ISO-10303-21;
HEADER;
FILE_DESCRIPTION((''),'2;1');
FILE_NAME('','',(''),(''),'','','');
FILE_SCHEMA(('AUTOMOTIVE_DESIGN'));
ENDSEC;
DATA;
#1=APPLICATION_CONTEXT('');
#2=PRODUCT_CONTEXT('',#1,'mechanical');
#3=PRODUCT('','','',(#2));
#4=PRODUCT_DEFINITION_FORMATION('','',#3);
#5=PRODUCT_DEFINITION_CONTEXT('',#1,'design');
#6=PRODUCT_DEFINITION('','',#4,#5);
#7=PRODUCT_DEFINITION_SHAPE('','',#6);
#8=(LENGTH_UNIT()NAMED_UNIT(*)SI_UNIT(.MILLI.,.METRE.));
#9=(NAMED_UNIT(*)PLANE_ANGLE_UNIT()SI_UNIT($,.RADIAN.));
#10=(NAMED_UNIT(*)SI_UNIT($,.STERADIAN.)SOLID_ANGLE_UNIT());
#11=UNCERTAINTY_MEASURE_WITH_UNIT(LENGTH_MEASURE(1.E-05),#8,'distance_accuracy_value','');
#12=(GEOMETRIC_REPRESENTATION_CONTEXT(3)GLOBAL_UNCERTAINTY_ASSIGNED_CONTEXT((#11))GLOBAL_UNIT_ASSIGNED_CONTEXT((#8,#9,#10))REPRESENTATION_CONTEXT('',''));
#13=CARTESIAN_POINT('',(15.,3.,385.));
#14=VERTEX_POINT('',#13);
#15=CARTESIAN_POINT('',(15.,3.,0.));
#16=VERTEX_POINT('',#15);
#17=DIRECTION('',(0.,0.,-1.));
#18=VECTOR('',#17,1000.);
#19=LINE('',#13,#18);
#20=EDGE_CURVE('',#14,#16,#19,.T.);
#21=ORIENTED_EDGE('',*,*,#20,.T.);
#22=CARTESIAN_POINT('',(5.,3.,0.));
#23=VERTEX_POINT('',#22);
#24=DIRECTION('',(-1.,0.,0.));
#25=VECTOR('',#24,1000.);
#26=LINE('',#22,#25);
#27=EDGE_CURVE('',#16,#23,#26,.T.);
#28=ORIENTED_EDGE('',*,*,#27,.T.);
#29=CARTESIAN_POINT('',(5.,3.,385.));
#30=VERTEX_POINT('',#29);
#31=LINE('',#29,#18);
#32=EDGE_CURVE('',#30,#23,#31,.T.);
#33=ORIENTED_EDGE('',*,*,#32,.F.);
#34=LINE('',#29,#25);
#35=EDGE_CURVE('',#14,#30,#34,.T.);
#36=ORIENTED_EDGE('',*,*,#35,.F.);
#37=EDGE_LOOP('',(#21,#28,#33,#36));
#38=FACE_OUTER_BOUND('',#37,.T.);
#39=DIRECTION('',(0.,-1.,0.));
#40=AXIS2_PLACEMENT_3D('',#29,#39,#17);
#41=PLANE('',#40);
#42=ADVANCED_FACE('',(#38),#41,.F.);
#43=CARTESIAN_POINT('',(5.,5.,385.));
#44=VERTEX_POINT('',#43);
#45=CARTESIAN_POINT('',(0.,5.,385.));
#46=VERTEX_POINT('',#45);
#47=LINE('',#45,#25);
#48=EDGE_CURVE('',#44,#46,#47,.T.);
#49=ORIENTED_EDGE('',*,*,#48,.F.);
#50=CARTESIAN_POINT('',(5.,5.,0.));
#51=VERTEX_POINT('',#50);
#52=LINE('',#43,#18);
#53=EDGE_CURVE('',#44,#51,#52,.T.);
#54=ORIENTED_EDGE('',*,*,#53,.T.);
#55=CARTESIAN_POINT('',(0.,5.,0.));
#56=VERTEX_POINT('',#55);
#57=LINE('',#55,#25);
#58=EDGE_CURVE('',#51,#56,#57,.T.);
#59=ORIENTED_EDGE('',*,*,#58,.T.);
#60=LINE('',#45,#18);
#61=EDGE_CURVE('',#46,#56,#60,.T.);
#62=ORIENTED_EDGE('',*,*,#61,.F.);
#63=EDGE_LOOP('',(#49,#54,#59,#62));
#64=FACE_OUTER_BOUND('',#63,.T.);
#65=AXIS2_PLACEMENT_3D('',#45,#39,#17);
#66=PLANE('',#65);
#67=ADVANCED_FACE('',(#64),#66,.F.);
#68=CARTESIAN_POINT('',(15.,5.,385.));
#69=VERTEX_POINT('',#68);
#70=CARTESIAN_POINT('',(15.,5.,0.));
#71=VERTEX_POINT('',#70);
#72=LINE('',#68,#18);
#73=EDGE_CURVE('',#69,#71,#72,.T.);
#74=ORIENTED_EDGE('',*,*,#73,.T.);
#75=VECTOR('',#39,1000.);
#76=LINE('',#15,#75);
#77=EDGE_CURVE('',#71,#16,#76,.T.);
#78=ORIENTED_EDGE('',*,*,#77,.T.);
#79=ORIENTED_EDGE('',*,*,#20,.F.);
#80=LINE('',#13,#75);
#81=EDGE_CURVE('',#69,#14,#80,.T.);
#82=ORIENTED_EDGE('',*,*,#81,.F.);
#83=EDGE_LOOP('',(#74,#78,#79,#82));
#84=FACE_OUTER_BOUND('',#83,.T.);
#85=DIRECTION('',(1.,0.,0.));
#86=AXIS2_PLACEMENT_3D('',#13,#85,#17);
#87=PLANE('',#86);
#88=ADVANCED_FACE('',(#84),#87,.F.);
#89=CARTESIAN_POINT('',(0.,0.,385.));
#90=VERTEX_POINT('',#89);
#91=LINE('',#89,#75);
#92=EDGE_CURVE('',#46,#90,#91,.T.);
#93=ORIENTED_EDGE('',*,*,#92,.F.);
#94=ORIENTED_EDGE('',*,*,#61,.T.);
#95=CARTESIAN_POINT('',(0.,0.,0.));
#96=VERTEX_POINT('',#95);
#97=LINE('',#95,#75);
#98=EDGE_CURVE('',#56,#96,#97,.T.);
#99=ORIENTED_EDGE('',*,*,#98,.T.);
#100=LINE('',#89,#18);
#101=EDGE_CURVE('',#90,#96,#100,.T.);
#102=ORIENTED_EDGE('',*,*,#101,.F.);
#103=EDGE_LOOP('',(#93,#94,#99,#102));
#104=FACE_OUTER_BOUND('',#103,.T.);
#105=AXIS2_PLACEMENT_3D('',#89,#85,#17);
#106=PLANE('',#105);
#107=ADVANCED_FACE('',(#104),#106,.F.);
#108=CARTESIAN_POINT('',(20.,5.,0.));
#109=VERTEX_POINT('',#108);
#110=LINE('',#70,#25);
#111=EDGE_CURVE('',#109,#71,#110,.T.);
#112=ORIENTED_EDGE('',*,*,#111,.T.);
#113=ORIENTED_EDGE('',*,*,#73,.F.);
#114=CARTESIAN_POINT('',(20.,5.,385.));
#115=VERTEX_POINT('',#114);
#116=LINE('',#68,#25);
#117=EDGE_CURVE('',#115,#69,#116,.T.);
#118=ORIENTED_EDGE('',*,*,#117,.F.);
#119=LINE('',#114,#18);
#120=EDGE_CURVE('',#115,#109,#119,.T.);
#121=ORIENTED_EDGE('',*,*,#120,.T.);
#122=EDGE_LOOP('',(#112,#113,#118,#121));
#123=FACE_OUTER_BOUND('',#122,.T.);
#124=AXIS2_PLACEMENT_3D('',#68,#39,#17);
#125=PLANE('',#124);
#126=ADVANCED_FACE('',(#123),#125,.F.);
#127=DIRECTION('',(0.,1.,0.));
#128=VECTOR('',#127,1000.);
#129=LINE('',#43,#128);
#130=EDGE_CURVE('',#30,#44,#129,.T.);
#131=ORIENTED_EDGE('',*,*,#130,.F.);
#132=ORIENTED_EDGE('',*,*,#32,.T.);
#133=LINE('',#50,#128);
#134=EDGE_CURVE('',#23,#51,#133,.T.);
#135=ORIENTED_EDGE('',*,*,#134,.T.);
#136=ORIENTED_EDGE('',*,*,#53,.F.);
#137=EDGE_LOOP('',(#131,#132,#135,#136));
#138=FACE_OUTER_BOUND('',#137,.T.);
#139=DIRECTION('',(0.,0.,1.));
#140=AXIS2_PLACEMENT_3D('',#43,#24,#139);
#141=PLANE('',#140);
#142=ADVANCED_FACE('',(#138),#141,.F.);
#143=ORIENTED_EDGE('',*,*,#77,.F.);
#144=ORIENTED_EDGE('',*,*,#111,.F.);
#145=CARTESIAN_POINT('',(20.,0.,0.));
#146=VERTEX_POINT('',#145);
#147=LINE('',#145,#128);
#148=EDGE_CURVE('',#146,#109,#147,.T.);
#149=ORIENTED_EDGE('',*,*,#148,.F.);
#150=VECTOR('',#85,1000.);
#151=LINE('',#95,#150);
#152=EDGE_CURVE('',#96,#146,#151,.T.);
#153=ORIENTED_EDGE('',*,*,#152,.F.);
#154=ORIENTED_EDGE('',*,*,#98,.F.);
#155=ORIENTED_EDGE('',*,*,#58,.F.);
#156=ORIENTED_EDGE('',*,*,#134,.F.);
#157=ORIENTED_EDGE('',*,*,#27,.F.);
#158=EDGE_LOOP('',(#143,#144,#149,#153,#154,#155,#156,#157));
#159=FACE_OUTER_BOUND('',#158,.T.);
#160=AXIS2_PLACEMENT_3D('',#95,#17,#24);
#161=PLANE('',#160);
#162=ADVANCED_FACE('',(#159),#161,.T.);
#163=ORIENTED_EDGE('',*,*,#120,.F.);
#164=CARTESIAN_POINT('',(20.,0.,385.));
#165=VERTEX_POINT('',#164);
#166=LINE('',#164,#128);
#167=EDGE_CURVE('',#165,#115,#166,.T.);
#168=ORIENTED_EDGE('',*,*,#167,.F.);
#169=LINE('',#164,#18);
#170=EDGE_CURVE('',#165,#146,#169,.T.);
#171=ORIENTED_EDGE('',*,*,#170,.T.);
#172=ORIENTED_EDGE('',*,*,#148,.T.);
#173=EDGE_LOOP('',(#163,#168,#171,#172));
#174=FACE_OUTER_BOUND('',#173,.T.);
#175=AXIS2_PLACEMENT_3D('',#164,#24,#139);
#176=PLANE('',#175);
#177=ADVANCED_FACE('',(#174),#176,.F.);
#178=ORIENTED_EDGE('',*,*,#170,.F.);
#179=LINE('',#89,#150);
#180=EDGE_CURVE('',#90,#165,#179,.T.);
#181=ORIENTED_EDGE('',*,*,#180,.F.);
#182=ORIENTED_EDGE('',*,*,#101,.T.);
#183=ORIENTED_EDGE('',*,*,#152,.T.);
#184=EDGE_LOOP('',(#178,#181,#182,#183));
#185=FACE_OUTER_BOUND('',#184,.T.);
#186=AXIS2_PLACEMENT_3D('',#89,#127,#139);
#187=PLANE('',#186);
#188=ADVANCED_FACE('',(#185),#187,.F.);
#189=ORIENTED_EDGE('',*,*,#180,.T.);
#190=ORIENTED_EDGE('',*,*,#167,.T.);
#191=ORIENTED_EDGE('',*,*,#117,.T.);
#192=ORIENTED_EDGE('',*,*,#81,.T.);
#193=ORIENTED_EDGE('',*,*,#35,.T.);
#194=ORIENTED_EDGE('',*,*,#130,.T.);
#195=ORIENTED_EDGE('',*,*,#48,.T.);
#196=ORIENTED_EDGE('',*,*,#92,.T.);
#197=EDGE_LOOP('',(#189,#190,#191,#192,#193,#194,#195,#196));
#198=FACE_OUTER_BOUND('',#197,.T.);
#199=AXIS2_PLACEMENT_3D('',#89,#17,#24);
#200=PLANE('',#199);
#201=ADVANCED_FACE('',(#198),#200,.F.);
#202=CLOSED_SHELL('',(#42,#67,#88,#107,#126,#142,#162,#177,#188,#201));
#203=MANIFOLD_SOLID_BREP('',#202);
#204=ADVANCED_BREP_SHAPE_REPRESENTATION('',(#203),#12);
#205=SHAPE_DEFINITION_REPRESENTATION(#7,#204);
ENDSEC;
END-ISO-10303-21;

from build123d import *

# Parameters (mm, degrees)
BOSS_EXTRUDE1_DEPTH = 385


with BuildPart() as part:
    # Sketch1 → Boss-Extrude1 (new body)
    with BuildSketch(Plane.XY):
        Polygon((5, 5), (5, 3), (15, 3), (15, 5), (20, 5), (20, 0), (0, 0), (0, 5), align=None)
    extrude(amount=BOSS_EXTRUDE1_DEPTH)


solid = part.part
